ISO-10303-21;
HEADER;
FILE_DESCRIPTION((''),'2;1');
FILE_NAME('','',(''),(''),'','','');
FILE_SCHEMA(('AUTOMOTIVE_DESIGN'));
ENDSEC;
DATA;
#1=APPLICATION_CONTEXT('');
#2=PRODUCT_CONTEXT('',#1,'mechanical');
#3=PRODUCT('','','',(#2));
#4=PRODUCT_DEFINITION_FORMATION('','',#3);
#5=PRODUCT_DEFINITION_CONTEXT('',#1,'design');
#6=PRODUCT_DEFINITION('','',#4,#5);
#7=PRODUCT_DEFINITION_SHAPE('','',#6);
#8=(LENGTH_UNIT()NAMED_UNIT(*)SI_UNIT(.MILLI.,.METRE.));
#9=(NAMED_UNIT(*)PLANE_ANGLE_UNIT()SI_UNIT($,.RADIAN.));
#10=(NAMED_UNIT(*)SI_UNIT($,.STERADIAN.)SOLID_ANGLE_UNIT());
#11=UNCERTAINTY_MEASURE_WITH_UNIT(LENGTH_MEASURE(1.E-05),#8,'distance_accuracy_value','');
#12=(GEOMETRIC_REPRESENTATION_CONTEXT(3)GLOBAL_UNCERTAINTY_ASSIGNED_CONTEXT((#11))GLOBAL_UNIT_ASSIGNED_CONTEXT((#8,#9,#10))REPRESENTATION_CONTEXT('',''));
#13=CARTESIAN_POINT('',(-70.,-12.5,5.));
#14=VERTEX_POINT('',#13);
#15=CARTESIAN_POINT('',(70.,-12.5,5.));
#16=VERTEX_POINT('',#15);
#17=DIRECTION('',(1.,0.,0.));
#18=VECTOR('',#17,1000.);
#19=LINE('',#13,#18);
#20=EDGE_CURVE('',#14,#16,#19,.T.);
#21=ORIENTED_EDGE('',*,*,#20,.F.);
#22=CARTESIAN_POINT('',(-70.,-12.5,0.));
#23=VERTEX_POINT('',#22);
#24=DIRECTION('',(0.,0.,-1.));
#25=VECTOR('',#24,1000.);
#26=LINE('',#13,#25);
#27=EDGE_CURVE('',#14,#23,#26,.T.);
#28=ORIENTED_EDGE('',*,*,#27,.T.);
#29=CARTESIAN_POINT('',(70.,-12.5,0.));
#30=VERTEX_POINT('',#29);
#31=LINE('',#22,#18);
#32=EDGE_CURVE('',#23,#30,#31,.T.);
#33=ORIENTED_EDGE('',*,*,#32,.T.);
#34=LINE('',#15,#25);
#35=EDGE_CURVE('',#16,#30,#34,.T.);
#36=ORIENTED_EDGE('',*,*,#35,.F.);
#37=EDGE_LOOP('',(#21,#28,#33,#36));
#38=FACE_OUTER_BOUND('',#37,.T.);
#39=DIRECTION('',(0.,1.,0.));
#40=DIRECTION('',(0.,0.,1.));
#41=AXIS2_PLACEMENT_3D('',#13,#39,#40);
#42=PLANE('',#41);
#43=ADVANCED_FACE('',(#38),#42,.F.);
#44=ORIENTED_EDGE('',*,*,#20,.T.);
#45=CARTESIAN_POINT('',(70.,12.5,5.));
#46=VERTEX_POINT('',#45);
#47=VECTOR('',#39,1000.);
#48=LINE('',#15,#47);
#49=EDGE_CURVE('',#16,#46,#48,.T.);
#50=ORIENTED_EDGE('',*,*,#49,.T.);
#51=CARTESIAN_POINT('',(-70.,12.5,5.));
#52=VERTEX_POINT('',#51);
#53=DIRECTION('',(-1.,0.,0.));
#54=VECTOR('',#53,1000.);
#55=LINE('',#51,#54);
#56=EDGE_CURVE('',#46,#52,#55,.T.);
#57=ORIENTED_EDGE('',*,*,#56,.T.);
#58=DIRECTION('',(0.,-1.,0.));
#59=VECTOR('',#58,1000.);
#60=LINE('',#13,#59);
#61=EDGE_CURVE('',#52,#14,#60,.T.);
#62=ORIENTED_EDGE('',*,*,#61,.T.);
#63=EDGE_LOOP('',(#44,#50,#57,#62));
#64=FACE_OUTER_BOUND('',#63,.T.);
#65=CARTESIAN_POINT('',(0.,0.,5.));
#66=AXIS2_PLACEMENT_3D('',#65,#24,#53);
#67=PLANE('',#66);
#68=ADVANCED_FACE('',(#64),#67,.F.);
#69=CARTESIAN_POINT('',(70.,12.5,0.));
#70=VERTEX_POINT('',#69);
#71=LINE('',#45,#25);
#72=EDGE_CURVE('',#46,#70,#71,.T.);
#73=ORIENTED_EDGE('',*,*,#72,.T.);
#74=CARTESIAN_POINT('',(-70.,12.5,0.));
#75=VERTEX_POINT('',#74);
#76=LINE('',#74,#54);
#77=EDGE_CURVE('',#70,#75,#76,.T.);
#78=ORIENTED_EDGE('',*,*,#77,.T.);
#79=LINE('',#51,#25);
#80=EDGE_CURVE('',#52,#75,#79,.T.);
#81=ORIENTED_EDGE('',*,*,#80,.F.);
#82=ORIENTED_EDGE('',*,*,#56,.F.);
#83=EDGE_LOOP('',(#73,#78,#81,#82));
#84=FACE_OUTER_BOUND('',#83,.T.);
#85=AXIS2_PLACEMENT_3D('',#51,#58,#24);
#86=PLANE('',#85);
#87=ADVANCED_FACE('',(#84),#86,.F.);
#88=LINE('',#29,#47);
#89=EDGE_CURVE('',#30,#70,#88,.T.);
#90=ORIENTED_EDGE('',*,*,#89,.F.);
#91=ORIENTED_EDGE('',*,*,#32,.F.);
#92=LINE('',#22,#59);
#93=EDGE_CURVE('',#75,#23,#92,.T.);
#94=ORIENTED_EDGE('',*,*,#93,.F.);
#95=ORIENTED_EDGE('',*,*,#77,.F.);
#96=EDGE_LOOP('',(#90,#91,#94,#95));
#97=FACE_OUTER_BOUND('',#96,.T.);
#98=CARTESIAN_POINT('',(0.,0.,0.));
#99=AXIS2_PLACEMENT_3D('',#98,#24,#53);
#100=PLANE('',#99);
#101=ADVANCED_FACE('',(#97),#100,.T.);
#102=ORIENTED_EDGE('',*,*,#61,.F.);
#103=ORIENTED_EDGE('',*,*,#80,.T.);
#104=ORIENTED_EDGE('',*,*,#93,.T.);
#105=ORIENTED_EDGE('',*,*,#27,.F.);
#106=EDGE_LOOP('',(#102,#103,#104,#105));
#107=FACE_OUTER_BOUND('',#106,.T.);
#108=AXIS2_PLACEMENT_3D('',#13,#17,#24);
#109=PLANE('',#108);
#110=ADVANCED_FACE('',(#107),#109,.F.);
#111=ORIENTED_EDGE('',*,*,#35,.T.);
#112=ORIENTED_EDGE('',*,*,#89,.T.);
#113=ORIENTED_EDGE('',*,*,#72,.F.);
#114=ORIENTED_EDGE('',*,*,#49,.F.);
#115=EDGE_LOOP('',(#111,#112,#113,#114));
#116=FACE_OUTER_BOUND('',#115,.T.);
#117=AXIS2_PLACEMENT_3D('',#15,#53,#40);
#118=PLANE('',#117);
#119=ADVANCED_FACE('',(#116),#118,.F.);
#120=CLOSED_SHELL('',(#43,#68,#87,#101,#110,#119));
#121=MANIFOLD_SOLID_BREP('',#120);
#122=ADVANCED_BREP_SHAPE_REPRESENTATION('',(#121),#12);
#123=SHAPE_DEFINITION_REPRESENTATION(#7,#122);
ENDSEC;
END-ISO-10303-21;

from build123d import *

# Parameters (mm, degrees)
SKETCH_1_W      = 140
SKETCH_1_H      = 25
EXTRUDE_1_DEPTH = 5


with BuildPart() as part:
    # 草图1 → 凸台-拉伸1 (new body)
    with BuildSketch(Plane.XY):
        Rectangle(SKETCH_1_W, SKETCH_1_H)
    extrude(amount=EXTRUDE_1_DEPTH)


solid = part.part
